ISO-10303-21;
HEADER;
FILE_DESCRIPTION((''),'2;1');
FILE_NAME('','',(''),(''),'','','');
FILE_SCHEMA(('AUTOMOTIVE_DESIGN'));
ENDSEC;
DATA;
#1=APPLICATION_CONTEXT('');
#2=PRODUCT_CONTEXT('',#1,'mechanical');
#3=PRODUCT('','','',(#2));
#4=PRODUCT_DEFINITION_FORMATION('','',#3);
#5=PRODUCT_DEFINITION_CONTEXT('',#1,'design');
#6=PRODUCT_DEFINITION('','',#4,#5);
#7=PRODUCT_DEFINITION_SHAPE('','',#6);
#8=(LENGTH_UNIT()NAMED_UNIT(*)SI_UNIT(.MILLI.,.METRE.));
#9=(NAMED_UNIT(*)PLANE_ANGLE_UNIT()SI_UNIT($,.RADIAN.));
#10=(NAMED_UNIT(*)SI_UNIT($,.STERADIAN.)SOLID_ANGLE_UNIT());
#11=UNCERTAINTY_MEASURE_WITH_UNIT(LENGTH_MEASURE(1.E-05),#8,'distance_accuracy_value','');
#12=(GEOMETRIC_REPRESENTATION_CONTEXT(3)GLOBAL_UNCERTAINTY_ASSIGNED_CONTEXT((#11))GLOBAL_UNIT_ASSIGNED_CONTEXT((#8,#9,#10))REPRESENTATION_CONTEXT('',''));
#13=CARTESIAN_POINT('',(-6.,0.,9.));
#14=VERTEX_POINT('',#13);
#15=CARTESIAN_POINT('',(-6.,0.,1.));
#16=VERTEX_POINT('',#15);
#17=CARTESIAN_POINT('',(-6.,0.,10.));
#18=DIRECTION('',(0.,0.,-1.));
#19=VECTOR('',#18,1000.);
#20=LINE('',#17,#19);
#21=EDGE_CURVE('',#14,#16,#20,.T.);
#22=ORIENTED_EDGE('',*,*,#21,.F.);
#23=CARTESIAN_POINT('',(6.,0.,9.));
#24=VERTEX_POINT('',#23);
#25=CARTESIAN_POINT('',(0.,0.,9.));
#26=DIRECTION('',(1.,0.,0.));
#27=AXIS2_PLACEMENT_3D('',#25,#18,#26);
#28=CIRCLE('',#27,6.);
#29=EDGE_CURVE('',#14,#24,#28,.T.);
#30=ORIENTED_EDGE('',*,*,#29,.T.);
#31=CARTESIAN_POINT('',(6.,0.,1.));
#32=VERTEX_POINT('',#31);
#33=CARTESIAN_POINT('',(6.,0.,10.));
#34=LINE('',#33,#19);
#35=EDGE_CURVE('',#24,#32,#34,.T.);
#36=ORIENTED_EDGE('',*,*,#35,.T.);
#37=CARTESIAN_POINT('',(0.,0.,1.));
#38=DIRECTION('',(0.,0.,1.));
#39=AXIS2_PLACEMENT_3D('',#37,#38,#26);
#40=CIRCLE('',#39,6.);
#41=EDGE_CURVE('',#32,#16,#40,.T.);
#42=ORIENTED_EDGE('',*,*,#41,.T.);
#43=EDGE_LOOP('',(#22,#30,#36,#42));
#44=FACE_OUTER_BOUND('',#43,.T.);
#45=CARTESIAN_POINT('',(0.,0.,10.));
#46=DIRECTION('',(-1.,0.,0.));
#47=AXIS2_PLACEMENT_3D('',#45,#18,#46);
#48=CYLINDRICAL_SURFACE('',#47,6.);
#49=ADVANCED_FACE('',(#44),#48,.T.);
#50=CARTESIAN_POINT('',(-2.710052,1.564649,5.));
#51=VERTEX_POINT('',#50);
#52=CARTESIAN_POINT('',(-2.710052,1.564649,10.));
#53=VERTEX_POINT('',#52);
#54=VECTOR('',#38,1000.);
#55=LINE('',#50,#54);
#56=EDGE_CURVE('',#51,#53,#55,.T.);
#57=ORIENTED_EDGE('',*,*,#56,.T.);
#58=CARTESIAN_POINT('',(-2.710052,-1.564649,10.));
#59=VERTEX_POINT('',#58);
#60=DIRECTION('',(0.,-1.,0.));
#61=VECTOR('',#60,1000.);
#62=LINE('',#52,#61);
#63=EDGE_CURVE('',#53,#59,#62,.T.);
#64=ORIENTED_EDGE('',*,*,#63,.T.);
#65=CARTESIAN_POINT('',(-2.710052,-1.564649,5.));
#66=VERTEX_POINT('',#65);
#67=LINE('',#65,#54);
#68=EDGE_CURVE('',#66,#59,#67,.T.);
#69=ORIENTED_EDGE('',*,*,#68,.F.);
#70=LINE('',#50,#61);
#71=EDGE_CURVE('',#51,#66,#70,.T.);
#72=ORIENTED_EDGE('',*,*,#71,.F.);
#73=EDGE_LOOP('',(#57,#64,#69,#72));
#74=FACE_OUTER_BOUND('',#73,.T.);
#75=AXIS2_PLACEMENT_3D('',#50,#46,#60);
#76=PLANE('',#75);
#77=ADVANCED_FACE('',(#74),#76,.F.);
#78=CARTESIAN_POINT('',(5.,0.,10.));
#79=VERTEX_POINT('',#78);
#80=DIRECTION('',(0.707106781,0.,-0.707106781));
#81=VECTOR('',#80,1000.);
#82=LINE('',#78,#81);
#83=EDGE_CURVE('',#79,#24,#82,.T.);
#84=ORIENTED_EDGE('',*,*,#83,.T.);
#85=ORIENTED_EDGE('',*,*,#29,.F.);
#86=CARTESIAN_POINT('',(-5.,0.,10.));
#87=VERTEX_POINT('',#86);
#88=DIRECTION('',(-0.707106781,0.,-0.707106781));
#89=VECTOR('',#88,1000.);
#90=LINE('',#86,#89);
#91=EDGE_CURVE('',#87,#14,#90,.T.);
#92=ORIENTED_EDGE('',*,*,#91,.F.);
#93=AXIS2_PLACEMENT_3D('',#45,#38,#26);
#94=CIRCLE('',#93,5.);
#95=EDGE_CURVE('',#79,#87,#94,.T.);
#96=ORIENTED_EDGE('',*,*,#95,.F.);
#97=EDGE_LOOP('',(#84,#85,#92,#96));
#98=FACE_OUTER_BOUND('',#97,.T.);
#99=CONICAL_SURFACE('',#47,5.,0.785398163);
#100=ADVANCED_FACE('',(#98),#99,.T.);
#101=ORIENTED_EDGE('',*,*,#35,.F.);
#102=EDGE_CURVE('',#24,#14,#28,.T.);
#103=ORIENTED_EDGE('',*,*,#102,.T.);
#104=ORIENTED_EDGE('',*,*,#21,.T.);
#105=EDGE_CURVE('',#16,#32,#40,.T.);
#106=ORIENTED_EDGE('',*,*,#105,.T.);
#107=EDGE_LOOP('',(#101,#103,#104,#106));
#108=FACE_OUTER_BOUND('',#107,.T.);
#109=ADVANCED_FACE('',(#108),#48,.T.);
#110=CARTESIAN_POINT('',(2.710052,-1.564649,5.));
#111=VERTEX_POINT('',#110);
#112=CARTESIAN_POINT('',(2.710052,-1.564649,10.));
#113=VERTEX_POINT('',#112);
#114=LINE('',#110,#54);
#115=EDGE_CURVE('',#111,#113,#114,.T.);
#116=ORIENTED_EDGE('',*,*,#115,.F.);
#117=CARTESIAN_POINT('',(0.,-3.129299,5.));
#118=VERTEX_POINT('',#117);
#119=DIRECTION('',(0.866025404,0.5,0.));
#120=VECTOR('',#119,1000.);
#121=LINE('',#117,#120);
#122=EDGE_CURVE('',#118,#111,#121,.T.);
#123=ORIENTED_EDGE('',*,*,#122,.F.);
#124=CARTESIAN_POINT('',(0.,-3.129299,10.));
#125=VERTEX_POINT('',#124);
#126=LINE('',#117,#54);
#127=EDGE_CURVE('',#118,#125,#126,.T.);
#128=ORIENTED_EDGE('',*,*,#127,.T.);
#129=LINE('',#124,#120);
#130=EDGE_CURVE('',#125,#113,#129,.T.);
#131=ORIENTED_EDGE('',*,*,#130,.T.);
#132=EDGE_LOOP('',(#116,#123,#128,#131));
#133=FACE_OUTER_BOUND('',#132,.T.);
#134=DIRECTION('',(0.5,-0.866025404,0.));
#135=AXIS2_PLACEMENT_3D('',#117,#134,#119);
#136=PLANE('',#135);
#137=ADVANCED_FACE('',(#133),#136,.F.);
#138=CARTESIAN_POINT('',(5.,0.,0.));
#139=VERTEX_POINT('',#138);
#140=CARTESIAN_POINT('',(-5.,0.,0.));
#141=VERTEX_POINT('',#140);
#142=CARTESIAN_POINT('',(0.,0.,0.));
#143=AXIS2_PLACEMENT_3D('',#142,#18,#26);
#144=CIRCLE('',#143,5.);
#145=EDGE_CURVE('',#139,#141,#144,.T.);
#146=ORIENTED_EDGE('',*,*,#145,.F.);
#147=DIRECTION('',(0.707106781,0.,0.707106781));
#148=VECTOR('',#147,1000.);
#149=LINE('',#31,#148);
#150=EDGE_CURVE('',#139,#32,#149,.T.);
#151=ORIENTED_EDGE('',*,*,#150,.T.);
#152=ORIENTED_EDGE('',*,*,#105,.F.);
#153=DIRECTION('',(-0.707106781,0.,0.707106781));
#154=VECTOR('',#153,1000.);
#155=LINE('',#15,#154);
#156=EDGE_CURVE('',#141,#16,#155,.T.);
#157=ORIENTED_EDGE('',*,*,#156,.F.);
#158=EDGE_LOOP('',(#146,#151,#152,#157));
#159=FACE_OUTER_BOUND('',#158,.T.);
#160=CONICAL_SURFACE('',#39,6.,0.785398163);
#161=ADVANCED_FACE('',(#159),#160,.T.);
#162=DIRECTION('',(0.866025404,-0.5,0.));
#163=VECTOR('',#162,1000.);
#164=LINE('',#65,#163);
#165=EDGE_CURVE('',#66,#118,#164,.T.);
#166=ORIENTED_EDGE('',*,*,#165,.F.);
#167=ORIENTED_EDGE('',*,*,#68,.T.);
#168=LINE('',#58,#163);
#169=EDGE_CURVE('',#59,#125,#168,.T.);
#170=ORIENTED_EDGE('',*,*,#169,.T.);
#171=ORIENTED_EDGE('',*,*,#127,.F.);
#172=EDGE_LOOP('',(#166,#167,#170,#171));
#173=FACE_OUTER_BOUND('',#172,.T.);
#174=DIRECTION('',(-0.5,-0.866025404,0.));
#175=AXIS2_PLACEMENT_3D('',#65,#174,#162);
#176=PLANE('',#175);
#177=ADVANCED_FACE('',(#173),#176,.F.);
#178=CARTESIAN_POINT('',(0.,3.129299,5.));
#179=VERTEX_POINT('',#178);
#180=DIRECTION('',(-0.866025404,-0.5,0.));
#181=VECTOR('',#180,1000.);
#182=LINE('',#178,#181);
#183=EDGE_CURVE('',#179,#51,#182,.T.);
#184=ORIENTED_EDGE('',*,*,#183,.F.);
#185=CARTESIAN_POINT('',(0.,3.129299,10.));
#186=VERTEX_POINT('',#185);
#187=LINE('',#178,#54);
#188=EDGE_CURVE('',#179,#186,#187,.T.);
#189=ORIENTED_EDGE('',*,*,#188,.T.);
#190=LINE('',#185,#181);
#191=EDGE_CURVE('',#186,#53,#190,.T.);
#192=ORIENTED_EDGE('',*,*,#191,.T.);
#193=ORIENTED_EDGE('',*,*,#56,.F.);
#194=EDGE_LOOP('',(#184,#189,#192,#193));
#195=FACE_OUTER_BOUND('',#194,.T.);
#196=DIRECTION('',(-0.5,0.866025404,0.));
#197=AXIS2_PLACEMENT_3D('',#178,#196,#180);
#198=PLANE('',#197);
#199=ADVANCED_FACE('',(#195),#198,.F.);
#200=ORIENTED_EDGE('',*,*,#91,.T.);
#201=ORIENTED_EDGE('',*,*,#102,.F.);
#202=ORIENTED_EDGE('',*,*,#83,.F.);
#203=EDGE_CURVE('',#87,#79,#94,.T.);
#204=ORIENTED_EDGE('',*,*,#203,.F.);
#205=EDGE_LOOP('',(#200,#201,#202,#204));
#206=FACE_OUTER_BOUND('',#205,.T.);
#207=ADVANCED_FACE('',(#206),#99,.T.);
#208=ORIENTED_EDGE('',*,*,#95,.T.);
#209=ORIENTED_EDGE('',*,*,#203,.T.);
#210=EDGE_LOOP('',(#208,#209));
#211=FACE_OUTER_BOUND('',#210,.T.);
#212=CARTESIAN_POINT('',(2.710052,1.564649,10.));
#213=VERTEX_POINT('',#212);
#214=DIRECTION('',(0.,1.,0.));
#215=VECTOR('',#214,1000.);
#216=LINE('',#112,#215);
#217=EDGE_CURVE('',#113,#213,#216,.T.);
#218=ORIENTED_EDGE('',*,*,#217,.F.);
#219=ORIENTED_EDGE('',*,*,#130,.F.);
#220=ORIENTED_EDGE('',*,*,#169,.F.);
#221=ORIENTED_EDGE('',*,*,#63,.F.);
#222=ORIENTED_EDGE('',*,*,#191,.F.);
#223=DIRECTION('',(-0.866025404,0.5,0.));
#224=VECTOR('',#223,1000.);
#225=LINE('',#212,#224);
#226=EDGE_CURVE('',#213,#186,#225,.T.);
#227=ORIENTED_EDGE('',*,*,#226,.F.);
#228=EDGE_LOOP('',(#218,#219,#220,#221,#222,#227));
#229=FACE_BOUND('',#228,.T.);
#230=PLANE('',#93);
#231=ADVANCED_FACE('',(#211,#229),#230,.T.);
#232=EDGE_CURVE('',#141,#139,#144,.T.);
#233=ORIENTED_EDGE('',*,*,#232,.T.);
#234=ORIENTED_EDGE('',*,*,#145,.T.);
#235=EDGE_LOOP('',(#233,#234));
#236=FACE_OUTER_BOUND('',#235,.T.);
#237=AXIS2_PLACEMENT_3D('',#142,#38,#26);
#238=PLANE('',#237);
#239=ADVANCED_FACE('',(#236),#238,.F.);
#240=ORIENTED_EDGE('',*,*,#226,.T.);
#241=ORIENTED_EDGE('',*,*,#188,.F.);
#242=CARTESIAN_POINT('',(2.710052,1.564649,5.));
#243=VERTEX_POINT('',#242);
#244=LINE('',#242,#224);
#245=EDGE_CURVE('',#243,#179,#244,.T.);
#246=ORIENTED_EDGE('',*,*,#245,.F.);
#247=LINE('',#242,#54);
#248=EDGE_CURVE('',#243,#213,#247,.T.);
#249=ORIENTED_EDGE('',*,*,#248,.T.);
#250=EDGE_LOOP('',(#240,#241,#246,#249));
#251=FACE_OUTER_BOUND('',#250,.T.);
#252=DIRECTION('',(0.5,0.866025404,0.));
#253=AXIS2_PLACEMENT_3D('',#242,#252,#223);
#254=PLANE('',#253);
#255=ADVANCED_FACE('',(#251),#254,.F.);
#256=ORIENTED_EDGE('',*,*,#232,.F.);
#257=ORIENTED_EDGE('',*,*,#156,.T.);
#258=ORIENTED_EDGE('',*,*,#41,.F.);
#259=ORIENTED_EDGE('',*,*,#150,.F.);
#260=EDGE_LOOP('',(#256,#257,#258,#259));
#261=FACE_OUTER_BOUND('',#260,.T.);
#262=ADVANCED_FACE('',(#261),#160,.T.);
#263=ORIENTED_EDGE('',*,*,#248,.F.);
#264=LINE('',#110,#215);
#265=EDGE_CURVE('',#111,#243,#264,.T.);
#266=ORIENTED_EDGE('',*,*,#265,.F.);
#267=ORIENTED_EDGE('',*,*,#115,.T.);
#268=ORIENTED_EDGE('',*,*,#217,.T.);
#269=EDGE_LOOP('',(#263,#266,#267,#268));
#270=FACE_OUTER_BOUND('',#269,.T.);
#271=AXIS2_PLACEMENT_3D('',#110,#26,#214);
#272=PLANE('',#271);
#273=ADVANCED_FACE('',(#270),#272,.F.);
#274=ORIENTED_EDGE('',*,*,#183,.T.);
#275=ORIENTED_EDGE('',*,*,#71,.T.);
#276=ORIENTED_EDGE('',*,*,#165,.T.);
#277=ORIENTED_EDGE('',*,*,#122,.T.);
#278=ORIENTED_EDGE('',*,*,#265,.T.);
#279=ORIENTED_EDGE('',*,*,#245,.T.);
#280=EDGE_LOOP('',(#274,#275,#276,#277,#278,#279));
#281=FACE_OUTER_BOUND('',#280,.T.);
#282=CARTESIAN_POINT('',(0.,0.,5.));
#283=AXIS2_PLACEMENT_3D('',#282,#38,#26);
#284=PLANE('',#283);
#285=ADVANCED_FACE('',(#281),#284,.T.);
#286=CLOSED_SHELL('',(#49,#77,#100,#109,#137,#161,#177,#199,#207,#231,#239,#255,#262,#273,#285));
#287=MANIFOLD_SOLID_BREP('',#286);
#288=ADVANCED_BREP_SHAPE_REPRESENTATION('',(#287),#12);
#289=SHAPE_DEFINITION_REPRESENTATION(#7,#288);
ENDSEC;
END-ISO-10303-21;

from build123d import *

# Parameters (mm, degrees)
SKETCH1_R           = 6
BOSS_EXTRUDE1_DEPTH = 10
CUT_EXTRUDE1_DEPTH  = 5
CHAMFER1_SIZE       = 1


with BuildPart() as part:
    # Sketch1 → Boss-Extrude1 (new body)
    with BuildSketch(Plane.XY):
        Circle(SKETCH1_R)
    extrude(amount=BOSS_EXTRUDE1_DEPTH)

    # Sketch2 → Cut-Extrude1 (cut)
    with BuildSketch(Plane.XY.offset(10)):
        Polygon((0, 3.129298789), (-2.710052247, 1.564649395), (-2.710052247, -1.564649395), (0, -3.129298789), (2.710052247, -1.564649395), (2.710052247, 1.564649395), align=None)
    extrude(amount=-CUT_EXTRUDE1_DEPTH, mode=Mode.SUBTRACT)

    # Chamfer1
    chamfer1_edges = [part.edges().sort_by_distance(p)[0] for p in [
        (-6, 0, 0),
        (-6, 0, 10),
    ]]
    chamfer(chamfer1_edges, length=CHAMFER1_SIZE)


solid = part.part
